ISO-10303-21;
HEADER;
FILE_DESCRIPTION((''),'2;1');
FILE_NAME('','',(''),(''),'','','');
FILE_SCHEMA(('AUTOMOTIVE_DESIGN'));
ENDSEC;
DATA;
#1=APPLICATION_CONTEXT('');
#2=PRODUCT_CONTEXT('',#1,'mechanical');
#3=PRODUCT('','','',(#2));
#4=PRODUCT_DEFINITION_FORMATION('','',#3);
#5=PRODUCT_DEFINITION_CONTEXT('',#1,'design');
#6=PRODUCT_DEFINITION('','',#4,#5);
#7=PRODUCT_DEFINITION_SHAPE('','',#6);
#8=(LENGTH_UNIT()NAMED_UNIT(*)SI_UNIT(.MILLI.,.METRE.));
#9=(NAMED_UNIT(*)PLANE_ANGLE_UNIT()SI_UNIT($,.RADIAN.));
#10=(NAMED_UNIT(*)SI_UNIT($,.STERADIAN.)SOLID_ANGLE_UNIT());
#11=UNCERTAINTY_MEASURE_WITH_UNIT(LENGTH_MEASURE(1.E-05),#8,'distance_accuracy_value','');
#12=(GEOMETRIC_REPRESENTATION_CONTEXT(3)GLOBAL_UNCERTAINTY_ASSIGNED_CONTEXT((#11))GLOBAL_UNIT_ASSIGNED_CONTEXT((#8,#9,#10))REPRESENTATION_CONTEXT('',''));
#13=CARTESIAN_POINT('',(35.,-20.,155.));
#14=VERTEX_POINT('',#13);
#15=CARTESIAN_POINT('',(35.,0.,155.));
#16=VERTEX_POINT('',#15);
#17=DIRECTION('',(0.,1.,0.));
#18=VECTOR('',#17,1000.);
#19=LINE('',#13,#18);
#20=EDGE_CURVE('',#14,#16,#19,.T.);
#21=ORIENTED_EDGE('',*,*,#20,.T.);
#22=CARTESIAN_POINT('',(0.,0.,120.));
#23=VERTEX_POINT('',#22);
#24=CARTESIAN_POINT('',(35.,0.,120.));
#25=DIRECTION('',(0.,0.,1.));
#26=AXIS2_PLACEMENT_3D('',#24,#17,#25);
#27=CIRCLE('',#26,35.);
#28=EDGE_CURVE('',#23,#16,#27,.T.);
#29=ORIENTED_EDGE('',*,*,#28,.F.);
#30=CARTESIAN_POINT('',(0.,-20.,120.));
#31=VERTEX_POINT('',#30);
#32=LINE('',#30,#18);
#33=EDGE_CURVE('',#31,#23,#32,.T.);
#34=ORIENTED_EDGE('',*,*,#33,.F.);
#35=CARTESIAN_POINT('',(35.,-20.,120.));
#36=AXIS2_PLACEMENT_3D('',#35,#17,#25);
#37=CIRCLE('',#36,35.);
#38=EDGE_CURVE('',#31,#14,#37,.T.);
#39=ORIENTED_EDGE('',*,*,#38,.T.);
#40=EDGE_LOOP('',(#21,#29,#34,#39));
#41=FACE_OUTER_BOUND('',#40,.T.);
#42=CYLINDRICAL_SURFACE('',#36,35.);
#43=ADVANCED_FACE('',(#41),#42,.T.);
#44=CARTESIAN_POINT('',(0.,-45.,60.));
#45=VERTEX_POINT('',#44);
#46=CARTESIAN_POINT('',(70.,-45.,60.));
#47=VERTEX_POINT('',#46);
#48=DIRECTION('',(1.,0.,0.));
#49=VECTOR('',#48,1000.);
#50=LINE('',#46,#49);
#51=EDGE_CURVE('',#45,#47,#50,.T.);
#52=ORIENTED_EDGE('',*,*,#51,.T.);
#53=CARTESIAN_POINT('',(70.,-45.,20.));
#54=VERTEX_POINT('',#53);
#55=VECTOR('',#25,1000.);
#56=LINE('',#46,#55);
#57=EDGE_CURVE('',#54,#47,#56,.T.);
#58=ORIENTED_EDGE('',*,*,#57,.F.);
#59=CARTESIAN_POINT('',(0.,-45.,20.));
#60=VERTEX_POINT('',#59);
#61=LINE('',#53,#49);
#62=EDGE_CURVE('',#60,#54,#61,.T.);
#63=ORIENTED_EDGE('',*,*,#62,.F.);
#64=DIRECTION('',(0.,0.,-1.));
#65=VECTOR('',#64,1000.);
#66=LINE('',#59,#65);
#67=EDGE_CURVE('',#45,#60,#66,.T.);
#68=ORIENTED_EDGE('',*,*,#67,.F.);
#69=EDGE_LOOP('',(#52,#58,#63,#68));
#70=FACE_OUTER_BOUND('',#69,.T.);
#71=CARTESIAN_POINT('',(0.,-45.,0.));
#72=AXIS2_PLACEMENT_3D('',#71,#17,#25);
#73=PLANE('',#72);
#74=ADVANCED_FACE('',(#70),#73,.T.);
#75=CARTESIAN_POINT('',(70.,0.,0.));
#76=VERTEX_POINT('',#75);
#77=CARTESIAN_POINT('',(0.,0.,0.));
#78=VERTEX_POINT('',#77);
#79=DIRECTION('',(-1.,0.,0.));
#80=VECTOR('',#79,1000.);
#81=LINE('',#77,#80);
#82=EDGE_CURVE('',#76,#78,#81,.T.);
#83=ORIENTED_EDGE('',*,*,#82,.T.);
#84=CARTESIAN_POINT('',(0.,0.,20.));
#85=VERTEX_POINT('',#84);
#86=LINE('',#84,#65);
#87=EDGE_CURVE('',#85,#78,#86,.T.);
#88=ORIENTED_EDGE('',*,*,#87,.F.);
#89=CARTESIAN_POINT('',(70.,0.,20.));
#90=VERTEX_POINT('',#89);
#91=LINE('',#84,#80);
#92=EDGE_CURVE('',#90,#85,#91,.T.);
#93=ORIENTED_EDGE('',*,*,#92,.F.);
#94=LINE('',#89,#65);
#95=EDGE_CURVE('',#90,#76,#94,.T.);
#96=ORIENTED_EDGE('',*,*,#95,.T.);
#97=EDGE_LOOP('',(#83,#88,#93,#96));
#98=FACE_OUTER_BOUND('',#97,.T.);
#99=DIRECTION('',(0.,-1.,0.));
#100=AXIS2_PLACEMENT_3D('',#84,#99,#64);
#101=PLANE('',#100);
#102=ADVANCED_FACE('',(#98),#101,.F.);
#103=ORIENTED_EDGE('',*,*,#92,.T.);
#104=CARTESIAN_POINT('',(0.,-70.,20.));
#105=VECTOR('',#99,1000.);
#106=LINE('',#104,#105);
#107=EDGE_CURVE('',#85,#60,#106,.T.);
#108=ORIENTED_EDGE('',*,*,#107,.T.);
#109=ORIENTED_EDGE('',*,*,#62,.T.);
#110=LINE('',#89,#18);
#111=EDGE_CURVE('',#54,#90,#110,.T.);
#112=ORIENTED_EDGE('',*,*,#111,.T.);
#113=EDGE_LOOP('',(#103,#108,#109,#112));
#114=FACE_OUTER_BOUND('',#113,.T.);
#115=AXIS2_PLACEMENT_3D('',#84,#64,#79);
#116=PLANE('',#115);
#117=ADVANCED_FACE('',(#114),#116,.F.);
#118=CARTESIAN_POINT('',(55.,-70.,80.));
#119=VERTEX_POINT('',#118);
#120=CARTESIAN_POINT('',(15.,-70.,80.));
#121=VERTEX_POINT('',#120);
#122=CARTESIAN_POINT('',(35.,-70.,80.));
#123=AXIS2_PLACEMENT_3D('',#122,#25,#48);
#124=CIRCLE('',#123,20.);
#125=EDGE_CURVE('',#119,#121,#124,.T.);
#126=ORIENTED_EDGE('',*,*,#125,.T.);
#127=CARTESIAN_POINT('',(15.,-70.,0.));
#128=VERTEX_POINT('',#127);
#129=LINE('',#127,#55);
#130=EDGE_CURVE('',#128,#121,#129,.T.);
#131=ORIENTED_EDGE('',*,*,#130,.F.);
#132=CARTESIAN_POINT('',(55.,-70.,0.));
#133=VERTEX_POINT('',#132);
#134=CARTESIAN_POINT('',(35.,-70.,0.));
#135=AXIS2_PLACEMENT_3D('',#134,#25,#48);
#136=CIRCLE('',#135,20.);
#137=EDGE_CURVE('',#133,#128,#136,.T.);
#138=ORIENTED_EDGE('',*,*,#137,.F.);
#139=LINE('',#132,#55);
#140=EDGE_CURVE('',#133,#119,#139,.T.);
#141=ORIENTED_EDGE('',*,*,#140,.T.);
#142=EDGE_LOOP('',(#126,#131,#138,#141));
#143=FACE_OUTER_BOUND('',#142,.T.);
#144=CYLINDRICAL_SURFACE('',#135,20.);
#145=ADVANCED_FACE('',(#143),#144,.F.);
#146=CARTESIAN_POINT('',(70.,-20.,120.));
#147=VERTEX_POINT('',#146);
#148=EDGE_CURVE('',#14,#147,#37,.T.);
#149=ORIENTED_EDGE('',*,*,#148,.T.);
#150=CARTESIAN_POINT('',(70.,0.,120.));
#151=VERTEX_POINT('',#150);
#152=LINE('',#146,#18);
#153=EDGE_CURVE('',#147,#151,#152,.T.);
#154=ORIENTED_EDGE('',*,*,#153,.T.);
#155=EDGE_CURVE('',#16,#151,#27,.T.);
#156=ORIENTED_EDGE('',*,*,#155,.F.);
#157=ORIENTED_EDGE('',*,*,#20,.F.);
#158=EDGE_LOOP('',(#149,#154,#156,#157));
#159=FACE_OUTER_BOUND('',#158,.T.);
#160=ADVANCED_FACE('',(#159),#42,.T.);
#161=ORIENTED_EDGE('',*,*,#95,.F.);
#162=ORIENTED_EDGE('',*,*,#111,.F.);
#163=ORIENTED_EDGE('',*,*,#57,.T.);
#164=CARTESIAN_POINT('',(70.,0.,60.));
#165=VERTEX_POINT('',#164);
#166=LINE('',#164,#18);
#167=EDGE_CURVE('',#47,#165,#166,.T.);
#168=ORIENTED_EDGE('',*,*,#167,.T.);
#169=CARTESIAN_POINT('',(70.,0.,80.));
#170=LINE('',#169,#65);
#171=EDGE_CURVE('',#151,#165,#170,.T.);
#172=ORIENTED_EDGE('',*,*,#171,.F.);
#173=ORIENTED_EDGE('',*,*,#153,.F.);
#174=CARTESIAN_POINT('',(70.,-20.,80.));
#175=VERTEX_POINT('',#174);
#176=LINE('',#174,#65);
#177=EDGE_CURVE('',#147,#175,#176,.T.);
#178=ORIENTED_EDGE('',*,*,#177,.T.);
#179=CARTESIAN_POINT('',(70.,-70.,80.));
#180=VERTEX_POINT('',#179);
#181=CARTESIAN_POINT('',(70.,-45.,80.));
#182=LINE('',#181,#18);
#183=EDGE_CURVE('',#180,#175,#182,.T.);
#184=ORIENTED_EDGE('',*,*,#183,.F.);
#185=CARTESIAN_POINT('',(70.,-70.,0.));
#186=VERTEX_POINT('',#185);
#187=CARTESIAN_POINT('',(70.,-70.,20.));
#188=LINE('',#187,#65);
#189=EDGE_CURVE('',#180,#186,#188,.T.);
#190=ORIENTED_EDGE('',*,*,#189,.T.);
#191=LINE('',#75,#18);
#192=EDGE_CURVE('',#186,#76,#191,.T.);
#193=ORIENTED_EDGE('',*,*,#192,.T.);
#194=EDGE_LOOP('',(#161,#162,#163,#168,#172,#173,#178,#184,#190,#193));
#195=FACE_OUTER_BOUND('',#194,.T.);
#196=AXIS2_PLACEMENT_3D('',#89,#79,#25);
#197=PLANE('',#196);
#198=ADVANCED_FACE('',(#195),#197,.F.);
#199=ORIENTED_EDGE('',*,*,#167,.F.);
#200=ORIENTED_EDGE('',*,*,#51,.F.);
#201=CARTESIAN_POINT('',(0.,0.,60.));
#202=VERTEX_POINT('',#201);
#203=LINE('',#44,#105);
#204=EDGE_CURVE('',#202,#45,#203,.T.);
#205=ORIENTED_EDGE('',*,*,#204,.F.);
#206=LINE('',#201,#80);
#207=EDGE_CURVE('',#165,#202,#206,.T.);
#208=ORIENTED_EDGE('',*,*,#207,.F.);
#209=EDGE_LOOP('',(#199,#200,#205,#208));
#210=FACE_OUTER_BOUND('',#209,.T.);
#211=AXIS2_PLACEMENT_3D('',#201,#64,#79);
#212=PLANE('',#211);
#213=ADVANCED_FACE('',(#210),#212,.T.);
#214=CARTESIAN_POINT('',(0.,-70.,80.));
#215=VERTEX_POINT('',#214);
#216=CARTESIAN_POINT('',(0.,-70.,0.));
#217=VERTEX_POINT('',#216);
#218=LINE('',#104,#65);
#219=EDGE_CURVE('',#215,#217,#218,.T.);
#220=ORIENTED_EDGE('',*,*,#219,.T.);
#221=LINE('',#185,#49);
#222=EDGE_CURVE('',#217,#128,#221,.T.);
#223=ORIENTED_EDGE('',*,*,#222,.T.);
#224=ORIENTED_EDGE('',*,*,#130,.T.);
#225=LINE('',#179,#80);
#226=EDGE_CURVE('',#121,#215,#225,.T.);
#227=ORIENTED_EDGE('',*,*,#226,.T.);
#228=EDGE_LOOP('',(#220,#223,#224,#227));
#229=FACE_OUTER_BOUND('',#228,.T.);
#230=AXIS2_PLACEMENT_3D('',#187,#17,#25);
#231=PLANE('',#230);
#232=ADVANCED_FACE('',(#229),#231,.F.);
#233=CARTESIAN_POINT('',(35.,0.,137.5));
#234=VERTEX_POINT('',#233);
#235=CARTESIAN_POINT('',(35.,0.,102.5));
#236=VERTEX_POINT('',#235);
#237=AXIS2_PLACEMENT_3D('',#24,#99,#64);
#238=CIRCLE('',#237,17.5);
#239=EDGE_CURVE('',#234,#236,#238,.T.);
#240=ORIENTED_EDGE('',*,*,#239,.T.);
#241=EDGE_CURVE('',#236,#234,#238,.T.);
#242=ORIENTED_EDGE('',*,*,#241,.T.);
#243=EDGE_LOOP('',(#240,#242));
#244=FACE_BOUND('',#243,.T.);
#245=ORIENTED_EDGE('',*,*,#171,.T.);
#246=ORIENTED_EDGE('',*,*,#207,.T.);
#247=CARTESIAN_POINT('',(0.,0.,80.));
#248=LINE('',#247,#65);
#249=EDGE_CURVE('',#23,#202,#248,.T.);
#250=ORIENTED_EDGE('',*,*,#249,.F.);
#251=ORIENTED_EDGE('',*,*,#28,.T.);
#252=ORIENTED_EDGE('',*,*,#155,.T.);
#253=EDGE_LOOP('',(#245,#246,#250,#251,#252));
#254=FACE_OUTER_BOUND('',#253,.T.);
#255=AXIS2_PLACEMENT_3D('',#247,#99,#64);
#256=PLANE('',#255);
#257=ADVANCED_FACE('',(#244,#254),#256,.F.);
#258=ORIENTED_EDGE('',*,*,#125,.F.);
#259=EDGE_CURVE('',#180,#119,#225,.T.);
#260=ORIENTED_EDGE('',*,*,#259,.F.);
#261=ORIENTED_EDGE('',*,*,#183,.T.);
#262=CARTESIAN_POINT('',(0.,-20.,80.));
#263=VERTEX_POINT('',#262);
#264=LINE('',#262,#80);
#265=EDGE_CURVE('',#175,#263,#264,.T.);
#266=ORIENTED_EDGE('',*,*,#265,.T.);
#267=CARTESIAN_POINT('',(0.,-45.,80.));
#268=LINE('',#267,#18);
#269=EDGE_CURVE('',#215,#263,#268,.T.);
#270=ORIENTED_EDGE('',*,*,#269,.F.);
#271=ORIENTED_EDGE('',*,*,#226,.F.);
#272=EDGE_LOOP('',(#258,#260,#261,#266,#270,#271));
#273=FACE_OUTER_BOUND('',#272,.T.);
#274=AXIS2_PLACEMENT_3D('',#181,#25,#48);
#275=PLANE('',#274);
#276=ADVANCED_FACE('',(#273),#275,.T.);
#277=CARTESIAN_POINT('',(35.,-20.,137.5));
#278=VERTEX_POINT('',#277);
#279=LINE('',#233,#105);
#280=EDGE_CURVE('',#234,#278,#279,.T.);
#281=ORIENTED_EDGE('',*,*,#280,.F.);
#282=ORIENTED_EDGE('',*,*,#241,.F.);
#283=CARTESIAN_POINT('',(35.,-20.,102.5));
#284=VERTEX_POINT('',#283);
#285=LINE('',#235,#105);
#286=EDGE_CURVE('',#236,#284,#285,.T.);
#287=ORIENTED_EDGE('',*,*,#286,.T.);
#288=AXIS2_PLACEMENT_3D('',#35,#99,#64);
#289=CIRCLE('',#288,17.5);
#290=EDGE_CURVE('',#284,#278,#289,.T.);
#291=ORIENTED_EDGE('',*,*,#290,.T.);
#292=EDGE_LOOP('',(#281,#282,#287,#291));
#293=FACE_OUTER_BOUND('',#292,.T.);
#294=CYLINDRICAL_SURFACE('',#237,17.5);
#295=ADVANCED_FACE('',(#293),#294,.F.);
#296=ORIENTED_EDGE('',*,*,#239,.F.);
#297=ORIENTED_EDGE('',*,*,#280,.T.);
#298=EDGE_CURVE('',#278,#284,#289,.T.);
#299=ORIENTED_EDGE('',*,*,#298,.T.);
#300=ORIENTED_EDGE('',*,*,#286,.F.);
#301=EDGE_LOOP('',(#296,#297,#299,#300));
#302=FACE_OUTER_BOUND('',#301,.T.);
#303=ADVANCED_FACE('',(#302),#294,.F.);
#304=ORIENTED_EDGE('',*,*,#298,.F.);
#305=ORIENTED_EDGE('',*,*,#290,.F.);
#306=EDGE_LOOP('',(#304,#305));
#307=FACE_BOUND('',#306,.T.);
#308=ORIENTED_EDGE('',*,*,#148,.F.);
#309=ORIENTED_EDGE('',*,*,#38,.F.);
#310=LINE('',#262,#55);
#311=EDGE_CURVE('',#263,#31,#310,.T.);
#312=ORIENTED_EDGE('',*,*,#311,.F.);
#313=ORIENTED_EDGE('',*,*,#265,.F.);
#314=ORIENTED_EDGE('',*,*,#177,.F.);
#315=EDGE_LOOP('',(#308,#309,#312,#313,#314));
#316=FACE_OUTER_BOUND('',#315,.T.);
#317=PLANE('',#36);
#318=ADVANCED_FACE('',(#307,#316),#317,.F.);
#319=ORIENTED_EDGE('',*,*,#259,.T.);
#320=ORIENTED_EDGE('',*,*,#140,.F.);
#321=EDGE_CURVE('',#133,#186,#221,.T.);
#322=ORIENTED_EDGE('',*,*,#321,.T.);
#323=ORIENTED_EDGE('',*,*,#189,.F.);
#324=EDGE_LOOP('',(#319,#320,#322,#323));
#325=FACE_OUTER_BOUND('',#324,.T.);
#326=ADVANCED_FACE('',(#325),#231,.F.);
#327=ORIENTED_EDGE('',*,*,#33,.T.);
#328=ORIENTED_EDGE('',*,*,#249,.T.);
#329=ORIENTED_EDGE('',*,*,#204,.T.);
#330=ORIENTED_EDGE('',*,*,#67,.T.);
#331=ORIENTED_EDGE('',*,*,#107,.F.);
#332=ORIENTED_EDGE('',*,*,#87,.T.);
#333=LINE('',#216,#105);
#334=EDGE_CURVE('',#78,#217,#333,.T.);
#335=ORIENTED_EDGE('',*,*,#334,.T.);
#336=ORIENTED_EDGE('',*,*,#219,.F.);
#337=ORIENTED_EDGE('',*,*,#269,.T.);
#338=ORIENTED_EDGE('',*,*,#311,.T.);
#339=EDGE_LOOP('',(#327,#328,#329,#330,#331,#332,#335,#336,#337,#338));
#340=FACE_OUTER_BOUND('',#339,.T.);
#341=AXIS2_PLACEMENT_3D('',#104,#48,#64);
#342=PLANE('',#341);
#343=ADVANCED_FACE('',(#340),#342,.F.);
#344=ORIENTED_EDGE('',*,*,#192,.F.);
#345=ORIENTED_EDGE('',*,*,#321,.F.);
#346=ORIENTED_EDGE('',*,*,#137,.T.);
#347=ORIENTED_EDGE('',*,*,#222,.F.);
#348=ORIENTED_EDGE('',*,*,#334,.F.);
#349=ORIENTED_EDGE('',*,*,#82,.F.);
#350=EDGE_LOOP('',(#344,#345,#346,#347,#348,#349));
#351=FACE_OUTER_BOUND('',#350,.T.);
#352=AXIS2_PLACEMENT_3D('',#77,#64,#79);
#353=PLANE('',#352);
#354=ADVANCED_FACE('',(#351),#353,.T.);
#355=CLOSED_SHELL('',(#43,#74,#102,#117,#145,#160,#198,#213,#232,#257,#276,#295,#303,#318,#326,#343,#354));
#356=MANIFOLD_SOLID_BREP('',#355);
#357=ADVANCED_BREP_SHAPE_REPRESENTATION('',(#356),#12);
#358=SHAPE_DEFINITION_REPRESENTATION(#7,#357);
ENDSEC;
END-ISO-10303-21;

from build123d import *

# Parameters (mm, degrees)
BASE_BLOCK_SKETCH_W   = 70
BASE_BLOCK_SKETCH_H   = 70
BASE_BLOCK_DEPTH      = 20
STEP_BLOCK_SKETCH_W   = 70
STEP_BLOCK_SKETCH_H   = 40
STEP_BLOCK_DEPTH      = 25
UPPER_BLOCK_SKETCH_W  = 70
UPPER_BLOCK_SKETCH_H  = 45
UPPER_BLOCK_DEPTH     = 20
UPRIGHT_WALL_SKETCH_W = 20
UPRIGHT_WALL_SKETCH_H = 25
UPRIGHT_WALL_DEPTH    = 70
ARC_RELIEF_CUT_DEPTH  = 80
ROUNDED_LUG_DEPTH     = 20
LUG_HOLE_SKETCH_R     = 17.5
LUG_HOLE_DEPTH        = 20


with BuildPart() as part:
    # Base Block Sketch → Base Block (new body)
    with BuildSketch(Plane.XY):
        with Locations((35, -35)):
            Rectangle(BASE_BLOCK_SKETCH_W, BASE_BLOCK_SKETCH_H)
    extrude(amount=BASE_BLOCK_DEPTH)

    # Step Block Sketch → Step Block (add)
    with BuildSketch(Plane.XZ.offset(70)):
        with Locations((35, 40)):
            Rectangle(STEP_BLOCK_SKETCH_W, STEP_BLOCK_SKETCH_H)
    extrude(amount=-STEP_BLOCK_DEPTH)



with BuildPart() as body_2:
    # Upper Block Sketch → Upper Block (new body)
    with BuildSketch(Plane.XY.offset(60)):
        with Locations((35, -22.5)):
            Rectangle(UPPER_BLOCK_SKETCH_W, UPPER_BLOCK_SKETCH_H)
    extrude(amount=UPPER_BLOCK_DEPTH)


with BuildPart() as part_1:
    add(part.part)

    add(body_2.part)  # Upright Wall merges body 2
    # Upright Wall Sketch → Upright Wall (add)
    with BuildSketch(Plane.ZY):
        with Locations((70, -57.5)):
            Rectangle(UPRIGHT_WALL_SKETCH_W, UPRIGHT_WALL_SKETCH_H)
    extrude(amount=-UPRIGHT_WALL_DEPTH)

    # Arc Relief Cut Sketch → Arc Relief Cut (cut)
    with BuildSketch(Plane.XY.offset(80)):
        with BuildLine():
            Line((15, -70), (55, -70))
            ThreePointArc((55, -70), (35, -50), (15, -70))
        make_face()
    extrude(amount=-ARC_RELIEF_CUT_DEPTH, mode=Mode.SUBTRACT)

    # Rounded Lug Sketch → Rounded Lug (add)
    with BuildSketch(Plane(origin=(0, 0, 0), x_dir=(1, 0, 0), z_dir=(0, 1, 0))):
        with BuildLine():
            Line((0, -80), (70, -80))
            Line((70, -80), (70, -120))
            ThreePointArc((70, -120), (35, -155), (0, -120))
            Line((0, -120), (0, -80))
        make_face()
    extrude(amount=-ROUNDED_LUG_DEPTH)

    # Lug Hole Sketch → Lug Hole (cut)
    with BuildSketch(Plane.XZ.offset(20)):
        with Locations(Location((35, 120, 0), (0, 0, 270))):
            Circle(LUG_HOLE_SKETCH_R)
    extrude(amount=-LUG_HOLE_DEPTH, mode=Mode.SUBTRACT)


solid = part_1.part
